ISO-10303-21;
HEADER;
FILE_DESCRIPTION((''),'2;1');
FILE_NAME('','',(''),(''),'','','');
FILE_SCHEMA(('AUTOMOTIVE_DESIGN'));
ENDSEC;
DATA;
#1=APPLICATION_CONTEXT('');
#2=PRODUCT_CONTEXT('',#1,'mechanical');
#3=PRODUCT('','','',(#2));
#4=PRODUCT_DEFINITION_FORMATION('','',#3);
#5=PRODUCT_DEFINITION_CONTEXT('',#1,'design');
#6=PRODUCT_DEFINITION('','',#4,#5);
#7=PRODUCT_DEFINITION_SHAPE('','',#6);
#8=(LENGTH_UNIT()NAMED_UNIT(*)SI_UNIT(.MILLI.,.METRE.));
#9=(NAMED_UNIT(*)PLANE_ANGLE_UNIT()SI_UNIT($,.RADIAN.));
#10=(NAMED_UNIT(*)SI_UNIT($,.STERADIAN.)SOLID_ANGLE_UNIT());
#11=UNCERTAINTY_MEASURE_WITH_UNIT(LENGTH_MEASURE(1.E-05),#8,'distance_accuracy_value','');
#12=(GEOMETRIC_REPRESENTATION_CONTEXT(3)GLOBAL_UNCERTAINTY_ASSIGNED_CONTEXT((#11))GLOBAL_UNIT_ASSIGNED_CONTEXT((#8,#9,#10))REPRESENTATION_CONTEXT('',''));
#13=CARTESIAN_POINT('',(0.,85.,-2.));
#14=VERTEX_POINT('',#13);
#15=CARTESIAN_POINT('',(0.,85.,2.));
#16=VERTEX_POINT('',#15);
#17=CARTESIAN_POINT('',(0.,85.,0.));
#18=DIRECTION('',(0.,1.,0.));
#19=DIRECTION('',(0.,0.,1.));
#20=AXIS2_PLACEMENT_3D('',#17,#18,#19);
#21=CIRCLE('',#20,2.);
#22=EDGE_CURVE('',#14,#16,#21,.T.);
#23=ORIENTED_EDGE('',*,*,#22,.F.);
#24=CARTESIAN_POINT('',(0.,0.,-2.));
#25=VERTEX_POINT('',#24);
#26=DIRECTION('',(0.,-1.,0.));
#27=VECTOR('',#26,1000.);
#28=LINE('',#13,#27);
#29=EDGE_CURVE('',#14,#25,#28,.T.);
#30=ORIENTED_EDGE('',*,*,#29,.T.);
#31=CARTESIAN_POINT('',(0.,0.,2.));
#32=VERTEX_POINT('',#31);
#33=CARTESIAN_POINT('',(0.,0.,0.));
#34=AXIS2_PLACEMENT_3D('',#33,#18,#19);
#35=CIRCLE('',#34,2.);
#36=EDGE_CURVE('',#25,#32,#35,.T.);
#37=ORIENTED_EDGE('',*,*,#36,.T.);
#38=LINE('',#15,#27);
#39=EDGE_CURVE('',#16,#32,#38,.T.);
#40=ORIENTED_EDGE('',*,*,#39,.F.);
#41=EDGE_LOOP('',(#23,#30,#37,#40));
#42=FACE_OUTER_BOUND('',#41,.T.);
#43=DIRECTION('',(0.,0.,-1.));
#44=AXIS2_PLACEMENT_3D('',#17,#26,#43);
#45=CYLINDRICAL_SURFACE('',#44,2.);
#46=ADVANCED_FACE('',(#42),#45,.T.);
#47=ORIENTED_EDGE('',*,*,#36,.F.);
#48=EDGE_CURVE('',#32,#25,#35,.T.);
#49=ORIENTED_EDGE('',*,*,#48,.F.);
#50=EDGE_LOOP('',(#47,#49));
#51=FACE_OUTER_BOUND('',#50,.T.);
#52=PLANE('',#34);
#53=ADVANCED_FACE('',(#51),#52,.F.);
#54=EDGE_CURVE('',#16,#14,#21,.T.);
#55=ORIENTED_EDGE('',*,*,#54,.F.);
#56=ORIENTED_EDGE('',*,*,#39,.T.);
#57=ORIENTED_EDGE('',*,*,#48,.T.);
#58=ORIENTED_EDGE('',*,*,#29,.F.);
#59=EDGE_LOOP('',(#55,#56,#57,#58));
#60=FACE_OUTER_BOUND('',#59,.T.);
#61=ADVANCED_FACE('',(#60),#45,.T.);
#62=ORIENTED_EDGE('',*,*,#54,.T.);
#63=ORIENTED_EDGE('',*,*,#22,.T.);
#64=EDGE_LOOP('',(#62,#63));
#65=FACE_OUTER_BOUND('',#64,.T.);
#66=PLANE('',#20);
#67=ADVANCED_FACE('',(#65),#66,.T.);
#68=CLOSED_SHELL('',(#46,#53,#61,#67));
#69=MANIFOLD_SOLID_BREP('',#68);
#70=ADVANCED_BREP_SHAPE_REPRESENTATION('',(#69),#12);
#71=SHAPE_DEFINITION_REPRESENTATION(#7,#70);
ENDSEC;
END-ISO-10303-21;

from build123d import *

# Parameters (mm, degrees)
SKETCH1_R           = 2
BOSS_EXTRUDE1_DEPTH = 85


with BuildPart() as part:
    # Sketch1 → Boss-Extrude1 (new body)
    with BuildSketch(Plane(origin=(0, 0, 0), x_dir=(1, 0, 0), z_dir=(0, 1, 0))):
        with Locations(Location((0, 0, 0), (0, 0, 270))):
            Circle(SKETCH1_R)
    extrude(amount=BOSS_EXTRUDE1_DEPTH)


solid = part.part
